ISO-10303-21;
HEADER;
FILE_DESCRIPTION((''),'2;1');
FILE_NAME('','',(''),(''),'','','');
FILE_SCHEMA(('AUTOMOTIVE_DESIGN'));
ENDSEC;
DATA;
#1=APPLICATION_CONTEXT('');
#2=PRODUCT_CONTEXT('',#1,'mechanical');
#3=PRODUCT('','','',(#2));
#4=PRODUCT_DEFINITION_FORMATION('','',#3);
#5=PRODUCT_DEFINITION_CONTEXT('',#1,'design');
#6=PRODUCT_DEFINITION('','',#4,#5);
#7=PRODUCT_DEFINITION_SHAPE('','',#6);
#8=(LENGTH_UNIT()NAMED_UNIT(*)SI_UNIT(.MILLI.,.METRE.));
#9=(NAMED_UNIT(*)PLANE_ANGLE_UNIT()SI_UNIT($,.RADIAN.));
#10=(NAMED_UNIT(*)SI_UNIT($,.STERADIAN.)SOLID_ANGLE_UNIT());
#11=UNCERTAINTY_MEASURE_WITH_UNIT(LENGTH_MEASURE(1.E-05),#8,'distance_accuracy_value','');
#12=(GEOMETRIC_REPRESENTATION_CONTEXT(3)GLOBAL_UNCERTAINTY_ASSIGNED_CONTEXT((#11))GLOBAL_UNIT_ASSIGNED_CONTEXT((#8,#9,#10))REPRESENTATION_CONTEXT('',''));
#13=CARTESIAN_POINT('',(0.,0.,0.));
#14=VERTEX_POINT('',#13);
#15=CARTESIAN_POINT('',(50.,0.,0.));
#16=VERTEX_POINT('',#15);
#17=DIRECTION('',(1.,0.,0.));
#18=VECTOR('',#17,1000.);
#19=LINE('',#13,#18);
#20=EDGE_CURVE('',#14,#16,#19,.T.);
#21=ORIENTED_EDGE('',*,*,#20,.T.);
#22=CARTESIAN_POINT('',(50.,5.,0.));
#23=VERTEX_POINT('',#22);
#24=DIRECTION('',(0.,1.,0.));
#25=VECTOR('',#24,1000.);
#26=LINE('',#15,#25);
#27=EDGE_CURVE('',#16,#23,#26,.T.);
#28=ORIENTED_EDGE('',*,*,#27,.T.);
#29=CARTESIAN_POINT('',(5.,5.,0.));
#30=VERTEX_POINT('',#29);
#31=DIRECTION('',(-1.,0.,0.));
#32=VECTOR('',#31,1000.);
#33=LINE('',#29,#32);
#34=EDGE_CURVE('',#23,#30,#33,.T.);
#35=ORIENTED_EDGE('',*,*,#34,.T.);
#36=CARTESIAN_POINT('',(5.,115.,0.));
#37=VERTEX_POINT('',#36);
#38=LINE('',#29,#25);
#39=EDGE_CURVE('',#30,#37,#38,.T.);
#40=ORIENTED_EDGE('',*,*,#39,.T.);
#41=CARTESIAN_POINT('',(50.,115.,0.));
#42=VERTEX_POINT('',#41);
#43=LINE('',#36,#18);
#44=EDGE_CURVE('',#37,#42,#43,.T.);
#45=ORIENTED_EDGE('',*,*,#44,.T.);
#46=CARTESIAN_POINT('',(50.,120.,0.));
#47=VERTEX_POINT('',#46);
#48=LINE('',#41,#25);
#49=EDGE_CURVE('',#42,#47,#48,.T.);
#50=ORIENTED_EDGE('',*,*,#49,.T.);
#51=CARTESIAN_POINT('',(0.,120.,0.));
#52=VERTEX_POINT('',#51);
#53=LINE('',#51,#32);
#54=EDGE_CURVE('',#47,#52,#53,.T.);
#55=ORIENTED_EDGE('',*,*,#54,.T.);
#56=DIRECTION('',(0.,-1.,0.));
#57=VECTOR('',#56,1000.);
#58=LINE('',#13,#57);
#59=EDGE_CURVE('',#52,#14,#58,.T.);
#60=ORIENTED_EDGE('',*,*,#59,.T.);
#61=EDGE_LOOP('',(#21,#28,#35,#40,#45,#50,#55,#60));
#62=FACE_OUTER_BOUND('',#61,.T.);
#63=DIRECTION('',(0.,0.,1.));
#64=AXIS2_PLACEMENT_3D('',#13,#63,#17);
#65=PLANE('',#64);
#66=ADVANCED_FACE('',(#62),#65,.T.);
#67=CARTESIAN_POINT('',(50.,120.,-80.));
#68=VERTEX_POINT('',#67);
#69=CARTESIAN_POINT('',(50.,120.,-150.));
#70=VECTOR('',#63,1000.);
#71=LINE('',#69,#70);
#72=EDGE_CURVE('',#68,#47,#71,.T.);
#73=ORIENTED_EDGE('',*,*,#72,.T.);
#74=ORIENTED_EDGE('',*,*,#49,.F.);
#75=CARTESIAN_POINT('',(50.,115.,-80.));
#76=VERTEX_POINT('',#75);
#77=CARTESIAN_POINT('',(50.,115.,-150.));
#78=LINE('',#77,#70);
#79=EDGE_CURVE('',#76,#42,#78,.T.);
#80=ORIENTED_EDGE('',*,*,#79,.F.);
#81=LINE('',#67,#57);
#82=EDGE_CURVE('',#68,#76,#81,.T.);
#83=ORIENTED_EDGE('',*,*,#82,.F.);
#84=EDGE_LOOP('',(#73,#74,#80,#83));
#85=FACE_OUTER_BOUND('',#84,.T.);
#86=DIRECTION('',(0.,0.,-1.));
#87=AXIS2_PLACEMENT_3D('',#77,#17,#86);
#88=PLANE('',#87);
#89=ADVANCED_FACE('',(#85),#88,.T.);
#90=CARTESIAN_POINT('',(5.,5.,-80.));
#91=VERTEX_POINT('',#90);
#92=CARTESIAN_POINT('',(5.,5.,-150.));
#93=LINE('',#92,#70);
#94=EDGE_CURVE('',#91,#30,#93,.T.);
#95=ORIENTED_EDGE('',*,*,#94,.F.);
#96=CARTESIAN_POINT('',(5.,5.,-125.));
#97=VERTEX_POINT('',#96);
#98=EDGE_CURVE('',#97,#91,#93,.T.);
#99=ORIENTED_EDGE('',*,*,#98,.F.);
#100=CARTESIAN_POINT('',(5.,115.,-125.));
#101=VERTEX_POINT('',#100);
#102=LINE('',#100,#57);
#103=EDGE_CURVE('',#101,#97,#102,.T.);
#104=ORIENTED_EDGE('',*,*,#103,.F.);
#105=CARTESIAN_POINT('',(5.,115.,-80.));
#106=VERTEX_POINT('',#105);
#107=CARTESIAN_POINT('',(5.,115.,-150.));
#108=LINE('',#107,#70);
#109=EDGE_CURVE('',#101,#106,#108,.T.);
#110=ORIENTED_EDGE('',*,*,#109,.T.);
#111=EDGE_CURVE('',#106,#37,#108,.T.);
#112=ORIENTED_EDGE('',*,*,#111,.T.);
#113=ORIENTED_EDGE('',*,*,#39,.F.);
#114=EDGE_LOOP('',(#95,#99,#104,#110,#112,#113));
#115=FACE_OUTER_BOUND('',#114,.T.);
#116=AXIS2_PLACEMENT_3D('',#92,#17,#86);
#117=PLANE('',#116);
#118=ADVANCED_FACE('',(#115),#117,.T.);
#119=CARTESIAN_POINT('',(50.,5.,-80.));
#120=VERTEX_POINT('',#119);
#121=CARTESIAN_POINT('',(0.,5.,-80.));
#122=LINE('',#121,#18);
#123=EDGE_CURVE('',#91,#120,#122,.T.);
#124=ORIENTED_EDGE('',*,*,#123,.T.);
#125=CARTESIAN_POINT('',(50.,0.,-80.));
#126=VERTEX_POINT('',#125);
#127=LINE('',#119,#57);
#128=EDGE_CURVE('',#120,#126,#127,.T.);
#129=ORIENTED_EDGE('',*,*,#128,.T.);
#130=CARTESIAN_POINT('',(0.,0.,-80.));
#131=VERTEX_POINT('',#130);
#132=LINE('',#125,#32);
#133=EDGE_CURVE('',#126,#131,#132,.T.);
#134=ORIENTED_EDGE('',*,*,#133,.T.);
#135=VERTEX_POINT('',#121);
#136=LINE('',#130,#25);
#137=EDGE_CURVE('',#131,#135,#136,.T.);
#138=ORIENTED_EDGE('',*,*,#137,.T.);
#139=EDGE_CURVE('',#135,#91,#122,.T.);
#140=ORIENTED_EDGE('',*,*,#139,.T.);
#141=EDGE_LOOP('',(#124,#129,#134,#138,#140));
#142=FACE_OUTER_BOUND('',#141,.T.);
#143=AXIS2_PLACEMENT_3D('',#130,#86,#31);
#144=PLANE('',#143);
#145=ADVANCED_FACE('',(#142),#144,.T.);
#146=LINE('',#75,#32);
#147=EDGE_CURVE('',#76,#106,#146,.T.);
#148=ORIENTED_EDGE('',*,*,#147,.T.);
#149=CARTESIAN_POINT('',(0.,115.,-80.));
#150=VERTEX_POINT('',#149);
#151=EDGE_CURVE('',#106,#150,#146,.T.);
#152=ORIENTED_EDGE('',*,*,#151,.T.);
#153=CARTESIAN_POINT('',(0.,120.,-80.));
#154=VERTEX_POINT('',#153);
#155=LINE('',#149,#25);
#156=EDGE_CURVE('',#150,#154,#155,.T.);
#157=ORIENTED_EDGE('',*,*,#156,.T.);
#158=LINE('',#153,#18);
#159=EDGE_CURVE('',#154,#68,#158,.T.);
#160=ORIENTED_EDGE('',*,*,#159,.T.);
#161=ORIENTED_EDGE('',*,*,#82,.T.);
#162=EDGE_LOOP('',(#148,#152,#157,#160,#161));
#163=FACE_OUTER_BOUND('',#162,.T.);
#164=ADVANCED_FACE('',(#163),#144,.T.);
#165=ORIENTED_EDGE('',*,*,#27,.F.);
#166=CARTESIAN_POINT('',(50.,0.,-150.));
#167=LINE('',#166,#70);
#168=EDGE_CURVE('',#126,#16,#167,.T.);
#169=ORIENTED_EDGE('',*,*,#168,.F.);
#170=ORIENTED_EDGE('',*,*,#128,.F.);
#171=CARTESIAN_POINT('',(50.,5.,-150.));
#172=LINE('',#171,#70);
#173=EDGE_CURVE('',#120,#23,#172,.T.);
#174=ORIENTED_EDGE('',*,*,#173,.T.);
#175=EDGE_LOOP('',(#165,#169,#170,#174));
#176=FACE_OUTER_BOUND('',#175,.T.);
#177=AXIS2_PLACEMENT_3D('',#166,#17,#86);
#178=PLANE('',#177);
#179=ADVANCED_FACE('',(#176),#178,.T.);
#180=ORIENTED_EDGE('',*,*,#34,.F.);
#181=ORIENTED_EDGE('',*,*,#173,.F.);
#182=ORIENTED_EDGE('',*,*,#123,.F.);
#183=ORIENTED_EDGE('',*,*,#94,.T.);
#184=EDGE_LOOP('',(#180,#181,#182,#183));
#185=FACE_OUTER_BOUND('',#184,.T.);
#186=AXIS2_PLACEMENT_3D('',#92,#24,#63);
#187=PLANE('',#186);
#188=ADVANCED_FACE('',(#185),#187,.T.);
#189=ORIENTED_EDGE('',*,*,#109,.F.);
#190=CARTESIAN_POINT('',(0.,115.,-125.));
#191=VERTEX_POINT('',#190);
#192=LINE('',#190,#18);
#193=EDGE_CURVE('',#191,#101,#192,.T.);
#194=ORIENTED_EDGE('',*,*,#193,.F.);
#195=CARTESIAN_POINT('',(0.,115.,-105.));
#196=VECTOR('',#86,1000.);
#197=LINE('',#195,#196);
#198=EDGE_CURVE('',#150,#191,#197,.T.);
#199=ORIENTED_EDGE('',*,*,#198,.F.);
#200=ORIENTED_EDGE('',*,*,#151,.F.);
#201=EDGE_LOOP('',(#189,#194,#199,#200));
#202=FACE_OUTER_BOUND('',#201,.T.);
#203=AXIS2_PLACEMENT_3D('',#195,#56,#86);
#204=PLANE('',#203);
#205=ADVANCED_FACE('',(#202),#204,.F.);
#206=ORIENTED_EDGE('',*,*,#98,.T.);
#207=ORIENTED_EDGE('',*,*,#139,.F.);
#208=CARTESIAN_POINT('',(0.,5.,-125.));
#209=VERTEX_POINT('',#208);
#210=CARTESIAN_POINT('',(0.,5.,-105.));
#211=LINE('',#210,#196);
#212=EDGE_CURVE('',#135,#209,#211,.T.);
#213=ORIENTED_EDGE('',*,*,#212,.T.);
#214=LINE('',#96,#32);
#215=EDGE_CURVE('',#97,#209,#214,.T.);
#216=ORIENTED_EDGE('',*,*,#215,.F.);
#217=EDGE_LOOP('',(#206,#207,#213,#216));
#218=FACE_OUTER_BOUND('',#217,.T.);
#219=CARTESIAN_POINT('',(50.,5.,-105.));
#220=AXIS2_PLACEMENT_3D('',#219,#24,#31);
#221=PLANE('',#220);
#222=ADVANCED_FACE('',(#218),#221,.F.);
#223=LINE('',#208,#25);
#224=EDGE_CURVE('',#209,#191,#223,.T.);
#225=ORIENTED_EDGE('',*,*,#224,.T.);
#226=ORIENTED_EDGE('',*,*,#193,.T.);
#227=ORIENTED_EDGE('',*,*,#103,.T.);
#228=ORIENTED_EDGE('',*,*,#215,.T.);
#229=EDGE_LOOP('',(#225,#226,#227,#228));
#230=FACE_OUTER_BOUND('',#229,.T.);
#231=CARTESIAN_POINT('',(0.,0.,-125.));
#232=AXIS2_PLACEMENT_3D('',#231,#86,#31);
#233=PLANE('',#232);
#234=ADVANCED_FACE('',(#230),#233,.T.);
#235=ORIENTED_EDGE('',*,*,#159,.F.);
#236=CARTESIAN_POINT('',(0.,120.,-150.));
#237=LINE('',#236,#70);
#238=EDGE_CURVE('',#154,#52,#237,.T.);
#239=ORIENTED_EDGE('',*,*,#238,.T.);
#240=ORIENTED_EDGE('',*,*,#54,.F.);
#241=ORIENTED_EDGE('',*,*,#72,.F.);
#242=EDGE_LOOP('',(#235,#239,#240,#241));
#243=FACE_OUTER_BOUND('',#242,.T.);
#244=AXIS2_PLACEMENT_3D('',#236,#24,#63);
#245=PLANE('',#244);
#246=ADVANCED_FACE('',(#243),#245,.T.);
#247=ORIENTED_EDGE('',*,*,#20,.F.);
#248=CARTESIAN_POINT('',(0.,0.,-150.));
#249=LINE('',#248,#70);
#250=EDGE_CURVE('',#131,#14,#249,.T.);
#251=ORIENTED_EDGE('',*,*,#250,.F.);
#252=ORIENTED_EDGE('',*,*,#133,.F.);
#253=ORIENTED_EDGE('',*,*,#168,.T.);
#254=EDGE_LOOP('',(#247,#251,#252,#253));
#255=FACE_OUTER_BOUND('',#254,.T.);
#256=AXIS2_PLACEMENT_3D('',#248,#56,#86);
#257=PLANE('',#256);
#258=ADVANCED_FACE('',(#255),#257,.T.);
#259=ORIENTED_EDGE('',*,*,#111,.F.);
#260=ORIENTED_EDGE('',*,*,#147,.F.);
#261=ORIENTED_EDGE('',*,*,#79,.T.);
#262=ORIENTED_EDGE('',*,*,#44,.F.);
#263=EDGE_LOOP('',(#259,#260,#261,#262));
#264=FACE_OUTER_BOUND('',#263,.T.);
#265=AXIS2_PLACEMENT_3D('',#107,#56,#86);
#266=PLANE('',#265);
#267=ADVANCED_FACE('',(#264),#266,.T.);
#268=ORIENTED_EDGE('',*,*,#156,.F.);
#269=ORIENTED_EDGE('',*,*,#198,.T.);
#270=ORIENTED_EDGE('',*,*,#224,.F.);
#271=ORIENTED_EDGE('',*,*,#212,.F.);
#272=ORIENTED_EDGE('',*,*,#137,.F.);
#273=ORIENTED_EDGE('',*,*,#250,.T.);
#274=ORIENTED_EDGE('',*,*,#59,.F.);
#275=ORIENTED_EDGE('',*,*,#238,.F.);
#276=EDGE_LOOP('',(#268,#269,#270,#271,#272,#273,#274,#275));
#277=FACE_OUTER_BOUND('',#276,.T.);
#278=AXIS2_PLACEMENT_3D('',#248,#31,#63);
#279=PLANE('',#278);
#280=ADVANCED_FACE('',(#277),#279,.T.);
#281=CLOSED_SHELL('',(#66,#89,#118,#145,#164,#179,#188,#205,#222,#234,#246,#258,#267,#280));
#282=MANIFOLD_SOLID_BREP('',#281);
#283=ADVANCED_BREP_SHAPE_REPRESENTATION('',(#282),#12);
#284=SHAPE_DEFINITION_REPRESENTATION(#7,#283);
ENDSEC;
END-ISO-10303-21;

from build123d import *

# Parameters (mm, degrees)
EXTRUDE_1_DEPTH     = 150
SKETCH_2_W          = 50
SKETCH_2_H          = 5
CUT_EXTRUDE_1_DEPTH = 45
SKETCH_3_W          = 5
SKETCH_3_H          = 110
CUT_EXTRUDE_2_DEPTH = 25
CUT_EXTRUDE_3_DEPTH = 25
CUT_EXTRUDE_4_DEPTH = 25


with BuildPart() as part:
    # 草图1 → 凸台-拉伸1 (new body)
    with BuildSketch(Plane.XY):
        Polygon((0, 0), (0, 120), (50, 120), (50, 115), (5, 115), (5, 5), (50, 5), (50, 0), align=None)
    extrude(amount=-EXTRUDE_1_DEPTH)

    # 草图2 → 切除-拉伸1 (cut)
    with BuildSketch(Plane(origin=(0, 0, -150), x_dir=(-1, 0, 0), z_dir=(0, 0, -1))):
        with Locations((-25, 117.5)):
            Rectangle(SKETCH_2_W, SKETCH_2_H)
        with Locations((-25, 2.5)):
            Rectangle(SKETCH_2_W, SKETCH_2_H)
    extrude(amount=-CUT_EXTRUDE_1_DEPTH, mode=Mode.SUBTRACT)

    # 草图3 → 切除-拉伸2 (cut)
    with BuildSketch(Plane(origin=(0, 0, -150), x_dir=(-1, 0, 0), z_dir=(0, 0, -1))):
        with Locations((-2.5, 60)):
            Rectangle(SKETCH_3_W, SKETCH_3_H)
    extrude(amount=-CUT_EXTRUDE_2_DEPTH, mode=Mode.SUBTRACT)

    # 草图4 → 切除-拉伸3 (cut)
    with BuildSketch(Plane(origin=(0, 0, -105), x_dir=(-1, 0, 0), z_dir=(0, 0, -1))):
        Polygon((-50, 0), (0, 0), (0, 5), (-5, 5), (-50, 5), align=None)
    extrude(amount=-CUT_EXTRUDE_3_DEPTH, mode=Mode.SUBTRACT)

    # 草图5 → 切除-拉伸4 (cut)
    with BuildSketch(Plane(origin=(0, 0, -105), x_dir=(-1, 0, 0), z_dir=(0, 0, -1))):
        Polygon((-50, 120), (-50, 115), (-5, 115), (0, 115), (0, 120), align=None)
    extrude(amount=-CUT_EXTRUDE_4_DEPTH, mode=Mode.SUBTRACT)


solid = part.part
